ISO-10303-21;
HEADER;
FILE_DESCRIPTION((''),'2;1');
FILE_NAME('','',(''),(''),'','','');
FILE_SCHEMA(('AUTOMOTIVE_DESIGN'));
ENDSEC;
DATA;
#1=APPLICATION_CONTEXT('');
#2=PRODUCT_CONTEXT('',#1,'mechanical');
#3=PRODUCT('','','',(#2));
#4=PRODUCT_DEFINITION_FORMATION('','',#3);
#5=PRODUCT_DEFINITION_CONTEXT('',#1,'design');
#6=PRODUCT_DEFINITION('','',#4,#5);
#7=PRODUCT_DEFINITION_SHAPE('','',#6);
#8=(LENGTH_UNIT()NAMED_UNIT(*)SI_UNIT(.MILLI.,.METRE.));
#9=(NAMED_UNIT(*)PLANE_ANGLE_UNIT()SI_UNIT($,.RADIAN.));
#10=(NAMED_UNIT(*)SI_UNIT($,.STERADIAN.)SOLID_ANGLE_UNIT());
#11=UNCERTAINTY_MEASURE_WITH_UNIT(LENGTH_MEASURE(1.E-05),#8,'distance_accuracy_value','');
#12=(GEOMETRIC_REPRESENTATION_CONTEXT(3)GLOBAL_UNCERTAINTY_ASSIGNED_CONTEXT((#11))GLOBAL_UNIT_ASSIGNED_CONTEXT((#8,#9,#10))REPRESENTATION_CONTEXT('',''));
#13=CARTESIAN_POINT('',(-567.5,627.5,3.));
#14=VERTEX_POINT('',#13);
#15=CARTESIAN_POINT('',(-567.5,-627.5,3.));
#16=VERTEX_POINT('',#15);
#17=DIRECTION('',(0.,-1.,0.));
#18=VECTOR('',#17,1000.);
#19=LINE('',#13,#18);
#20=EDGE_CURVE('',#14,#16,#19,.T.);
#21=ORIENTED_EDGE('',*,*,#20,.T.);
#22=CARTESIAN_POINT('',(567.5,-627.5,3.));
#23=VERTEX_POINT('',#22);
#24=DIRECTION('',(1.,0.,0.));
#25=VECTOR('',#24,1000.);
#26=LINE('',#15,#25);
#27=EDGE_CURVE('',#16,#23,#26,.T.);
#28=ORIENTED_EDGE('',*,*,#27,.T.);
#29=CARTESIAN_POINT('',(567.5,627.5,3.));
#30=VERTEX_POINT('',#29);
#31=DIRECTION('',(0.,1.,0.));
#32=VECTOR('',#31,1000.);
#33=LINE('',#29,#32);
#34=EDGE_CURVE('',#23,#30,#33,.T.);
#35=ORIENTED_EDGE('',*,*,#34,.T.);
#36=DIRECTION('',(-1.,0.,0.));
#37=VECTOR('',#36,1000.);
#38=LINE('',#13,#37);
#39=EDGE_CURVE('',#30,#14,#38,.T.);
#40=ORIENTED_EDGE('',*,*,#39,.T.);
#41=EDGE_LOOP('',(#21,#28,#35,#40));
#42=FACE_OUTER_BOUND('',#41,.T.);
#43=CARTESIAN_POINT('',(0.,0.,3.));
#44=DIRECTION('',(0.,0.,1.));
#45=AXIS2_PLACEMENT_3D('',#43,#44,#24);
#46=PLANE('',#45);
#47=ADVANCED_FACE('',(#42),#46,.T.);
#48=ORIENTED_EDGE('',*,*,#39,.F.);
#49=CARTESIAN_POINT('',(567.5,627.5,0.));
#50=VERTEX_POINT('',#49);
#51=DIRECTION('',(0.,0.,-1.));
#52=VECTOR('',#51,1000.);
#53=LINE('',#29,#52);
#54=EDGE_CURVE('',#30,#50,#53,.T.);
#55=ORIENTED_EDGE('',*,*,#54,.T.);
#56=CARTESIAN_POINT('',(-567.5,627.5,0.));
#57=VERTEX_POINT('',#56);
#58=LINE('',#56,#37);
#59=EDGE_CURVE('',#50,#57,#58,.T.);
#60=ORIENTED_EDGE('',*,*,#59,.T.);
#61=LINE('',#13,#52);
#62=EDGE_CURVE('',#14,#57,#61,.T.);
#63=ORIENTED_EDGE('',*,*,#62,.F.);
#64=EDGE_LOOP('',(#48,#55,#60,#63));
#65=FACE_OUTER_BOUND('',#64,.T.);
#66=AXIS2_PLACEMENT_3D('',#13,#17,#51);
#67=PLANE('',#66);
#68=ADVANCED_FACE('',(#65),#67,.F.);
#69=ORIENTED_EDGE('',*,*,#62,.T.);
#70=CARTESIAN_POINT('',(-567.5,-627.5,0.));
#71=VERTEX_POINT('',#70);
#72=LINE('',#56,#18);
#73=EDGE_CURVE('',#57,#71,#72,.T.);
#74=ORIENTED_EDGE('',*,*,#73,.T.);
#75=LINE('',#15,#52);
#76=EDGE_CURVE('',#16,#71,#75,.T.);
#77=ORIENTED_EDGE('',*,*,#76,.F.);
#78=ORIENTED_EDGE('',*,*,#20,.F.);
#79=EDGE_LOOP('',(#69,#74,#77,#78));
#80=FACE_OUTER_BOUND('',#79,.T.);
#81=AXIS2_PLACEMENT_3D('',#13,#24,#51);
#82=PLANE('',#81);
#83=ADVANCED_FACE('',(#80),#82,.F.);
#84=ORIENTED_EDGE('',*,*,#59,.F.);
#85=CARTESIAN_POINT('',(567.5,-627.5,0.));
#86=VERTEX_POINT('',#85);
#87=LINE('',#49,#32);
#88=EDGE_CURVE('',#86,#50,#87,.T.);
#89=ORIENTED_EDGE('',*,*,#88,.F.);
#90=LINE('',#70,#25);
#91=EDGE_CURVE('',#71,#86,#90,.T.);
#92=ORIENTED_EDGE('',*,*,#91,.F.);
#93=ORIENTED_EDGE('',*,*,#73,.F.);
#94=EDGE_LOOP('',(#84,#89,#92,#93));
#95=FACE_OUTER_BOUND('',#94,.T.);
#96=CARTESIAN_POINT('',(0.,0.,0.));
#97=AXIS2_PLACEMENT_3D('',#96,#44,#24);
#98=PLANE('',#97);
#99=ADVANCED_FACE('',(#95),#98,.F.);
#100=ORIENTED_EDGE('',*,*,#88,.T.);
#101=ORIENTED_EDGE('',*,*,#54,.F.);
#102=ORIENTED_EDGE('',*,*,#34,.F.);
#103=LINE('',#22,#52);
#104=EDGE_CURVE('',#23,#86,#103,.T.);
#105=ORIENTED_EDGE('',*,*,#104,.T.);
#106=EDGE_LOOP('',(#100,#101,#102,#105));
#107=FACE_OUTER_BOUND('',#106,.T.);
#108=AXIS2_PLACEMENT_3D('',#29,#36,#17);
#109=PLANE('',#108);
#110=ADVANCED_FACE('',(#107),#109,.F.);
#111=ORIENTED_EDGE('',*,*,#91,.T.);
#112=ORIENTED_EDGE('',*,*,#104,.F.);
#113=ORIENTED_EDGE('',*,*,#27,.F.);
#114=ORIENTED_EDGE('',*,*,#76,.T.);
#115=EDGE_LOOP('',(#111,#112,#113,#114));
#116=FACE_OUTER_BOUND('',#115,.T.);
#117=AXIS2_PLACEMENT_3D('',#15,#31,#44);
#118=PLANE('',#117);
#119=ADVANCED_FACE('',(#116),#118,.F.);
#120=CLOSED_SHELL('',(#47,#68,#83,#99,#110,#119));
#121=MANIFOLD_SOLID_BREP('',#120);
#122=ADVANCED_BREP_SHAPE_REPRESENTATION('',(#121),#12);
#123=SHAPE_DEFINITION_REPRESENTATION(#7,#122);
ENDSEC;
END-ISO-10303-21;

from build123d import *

# Parameters (mm, degrees)
SKETCH_1_W      = 1135
SKETCH_1_H      = 1255
EXTRUDE_1_DEPTH = 3


with BuildPart() as part:
    # 草图1 → 凸台-拉伸1 (new body)
    with BuildSketch(Plane.XY):
        Rectangle(SKETCH_1_W, SKETCH_1_H)
    extrude(amount=EXTRUDE_1_DEPTH)


solid = part.part
